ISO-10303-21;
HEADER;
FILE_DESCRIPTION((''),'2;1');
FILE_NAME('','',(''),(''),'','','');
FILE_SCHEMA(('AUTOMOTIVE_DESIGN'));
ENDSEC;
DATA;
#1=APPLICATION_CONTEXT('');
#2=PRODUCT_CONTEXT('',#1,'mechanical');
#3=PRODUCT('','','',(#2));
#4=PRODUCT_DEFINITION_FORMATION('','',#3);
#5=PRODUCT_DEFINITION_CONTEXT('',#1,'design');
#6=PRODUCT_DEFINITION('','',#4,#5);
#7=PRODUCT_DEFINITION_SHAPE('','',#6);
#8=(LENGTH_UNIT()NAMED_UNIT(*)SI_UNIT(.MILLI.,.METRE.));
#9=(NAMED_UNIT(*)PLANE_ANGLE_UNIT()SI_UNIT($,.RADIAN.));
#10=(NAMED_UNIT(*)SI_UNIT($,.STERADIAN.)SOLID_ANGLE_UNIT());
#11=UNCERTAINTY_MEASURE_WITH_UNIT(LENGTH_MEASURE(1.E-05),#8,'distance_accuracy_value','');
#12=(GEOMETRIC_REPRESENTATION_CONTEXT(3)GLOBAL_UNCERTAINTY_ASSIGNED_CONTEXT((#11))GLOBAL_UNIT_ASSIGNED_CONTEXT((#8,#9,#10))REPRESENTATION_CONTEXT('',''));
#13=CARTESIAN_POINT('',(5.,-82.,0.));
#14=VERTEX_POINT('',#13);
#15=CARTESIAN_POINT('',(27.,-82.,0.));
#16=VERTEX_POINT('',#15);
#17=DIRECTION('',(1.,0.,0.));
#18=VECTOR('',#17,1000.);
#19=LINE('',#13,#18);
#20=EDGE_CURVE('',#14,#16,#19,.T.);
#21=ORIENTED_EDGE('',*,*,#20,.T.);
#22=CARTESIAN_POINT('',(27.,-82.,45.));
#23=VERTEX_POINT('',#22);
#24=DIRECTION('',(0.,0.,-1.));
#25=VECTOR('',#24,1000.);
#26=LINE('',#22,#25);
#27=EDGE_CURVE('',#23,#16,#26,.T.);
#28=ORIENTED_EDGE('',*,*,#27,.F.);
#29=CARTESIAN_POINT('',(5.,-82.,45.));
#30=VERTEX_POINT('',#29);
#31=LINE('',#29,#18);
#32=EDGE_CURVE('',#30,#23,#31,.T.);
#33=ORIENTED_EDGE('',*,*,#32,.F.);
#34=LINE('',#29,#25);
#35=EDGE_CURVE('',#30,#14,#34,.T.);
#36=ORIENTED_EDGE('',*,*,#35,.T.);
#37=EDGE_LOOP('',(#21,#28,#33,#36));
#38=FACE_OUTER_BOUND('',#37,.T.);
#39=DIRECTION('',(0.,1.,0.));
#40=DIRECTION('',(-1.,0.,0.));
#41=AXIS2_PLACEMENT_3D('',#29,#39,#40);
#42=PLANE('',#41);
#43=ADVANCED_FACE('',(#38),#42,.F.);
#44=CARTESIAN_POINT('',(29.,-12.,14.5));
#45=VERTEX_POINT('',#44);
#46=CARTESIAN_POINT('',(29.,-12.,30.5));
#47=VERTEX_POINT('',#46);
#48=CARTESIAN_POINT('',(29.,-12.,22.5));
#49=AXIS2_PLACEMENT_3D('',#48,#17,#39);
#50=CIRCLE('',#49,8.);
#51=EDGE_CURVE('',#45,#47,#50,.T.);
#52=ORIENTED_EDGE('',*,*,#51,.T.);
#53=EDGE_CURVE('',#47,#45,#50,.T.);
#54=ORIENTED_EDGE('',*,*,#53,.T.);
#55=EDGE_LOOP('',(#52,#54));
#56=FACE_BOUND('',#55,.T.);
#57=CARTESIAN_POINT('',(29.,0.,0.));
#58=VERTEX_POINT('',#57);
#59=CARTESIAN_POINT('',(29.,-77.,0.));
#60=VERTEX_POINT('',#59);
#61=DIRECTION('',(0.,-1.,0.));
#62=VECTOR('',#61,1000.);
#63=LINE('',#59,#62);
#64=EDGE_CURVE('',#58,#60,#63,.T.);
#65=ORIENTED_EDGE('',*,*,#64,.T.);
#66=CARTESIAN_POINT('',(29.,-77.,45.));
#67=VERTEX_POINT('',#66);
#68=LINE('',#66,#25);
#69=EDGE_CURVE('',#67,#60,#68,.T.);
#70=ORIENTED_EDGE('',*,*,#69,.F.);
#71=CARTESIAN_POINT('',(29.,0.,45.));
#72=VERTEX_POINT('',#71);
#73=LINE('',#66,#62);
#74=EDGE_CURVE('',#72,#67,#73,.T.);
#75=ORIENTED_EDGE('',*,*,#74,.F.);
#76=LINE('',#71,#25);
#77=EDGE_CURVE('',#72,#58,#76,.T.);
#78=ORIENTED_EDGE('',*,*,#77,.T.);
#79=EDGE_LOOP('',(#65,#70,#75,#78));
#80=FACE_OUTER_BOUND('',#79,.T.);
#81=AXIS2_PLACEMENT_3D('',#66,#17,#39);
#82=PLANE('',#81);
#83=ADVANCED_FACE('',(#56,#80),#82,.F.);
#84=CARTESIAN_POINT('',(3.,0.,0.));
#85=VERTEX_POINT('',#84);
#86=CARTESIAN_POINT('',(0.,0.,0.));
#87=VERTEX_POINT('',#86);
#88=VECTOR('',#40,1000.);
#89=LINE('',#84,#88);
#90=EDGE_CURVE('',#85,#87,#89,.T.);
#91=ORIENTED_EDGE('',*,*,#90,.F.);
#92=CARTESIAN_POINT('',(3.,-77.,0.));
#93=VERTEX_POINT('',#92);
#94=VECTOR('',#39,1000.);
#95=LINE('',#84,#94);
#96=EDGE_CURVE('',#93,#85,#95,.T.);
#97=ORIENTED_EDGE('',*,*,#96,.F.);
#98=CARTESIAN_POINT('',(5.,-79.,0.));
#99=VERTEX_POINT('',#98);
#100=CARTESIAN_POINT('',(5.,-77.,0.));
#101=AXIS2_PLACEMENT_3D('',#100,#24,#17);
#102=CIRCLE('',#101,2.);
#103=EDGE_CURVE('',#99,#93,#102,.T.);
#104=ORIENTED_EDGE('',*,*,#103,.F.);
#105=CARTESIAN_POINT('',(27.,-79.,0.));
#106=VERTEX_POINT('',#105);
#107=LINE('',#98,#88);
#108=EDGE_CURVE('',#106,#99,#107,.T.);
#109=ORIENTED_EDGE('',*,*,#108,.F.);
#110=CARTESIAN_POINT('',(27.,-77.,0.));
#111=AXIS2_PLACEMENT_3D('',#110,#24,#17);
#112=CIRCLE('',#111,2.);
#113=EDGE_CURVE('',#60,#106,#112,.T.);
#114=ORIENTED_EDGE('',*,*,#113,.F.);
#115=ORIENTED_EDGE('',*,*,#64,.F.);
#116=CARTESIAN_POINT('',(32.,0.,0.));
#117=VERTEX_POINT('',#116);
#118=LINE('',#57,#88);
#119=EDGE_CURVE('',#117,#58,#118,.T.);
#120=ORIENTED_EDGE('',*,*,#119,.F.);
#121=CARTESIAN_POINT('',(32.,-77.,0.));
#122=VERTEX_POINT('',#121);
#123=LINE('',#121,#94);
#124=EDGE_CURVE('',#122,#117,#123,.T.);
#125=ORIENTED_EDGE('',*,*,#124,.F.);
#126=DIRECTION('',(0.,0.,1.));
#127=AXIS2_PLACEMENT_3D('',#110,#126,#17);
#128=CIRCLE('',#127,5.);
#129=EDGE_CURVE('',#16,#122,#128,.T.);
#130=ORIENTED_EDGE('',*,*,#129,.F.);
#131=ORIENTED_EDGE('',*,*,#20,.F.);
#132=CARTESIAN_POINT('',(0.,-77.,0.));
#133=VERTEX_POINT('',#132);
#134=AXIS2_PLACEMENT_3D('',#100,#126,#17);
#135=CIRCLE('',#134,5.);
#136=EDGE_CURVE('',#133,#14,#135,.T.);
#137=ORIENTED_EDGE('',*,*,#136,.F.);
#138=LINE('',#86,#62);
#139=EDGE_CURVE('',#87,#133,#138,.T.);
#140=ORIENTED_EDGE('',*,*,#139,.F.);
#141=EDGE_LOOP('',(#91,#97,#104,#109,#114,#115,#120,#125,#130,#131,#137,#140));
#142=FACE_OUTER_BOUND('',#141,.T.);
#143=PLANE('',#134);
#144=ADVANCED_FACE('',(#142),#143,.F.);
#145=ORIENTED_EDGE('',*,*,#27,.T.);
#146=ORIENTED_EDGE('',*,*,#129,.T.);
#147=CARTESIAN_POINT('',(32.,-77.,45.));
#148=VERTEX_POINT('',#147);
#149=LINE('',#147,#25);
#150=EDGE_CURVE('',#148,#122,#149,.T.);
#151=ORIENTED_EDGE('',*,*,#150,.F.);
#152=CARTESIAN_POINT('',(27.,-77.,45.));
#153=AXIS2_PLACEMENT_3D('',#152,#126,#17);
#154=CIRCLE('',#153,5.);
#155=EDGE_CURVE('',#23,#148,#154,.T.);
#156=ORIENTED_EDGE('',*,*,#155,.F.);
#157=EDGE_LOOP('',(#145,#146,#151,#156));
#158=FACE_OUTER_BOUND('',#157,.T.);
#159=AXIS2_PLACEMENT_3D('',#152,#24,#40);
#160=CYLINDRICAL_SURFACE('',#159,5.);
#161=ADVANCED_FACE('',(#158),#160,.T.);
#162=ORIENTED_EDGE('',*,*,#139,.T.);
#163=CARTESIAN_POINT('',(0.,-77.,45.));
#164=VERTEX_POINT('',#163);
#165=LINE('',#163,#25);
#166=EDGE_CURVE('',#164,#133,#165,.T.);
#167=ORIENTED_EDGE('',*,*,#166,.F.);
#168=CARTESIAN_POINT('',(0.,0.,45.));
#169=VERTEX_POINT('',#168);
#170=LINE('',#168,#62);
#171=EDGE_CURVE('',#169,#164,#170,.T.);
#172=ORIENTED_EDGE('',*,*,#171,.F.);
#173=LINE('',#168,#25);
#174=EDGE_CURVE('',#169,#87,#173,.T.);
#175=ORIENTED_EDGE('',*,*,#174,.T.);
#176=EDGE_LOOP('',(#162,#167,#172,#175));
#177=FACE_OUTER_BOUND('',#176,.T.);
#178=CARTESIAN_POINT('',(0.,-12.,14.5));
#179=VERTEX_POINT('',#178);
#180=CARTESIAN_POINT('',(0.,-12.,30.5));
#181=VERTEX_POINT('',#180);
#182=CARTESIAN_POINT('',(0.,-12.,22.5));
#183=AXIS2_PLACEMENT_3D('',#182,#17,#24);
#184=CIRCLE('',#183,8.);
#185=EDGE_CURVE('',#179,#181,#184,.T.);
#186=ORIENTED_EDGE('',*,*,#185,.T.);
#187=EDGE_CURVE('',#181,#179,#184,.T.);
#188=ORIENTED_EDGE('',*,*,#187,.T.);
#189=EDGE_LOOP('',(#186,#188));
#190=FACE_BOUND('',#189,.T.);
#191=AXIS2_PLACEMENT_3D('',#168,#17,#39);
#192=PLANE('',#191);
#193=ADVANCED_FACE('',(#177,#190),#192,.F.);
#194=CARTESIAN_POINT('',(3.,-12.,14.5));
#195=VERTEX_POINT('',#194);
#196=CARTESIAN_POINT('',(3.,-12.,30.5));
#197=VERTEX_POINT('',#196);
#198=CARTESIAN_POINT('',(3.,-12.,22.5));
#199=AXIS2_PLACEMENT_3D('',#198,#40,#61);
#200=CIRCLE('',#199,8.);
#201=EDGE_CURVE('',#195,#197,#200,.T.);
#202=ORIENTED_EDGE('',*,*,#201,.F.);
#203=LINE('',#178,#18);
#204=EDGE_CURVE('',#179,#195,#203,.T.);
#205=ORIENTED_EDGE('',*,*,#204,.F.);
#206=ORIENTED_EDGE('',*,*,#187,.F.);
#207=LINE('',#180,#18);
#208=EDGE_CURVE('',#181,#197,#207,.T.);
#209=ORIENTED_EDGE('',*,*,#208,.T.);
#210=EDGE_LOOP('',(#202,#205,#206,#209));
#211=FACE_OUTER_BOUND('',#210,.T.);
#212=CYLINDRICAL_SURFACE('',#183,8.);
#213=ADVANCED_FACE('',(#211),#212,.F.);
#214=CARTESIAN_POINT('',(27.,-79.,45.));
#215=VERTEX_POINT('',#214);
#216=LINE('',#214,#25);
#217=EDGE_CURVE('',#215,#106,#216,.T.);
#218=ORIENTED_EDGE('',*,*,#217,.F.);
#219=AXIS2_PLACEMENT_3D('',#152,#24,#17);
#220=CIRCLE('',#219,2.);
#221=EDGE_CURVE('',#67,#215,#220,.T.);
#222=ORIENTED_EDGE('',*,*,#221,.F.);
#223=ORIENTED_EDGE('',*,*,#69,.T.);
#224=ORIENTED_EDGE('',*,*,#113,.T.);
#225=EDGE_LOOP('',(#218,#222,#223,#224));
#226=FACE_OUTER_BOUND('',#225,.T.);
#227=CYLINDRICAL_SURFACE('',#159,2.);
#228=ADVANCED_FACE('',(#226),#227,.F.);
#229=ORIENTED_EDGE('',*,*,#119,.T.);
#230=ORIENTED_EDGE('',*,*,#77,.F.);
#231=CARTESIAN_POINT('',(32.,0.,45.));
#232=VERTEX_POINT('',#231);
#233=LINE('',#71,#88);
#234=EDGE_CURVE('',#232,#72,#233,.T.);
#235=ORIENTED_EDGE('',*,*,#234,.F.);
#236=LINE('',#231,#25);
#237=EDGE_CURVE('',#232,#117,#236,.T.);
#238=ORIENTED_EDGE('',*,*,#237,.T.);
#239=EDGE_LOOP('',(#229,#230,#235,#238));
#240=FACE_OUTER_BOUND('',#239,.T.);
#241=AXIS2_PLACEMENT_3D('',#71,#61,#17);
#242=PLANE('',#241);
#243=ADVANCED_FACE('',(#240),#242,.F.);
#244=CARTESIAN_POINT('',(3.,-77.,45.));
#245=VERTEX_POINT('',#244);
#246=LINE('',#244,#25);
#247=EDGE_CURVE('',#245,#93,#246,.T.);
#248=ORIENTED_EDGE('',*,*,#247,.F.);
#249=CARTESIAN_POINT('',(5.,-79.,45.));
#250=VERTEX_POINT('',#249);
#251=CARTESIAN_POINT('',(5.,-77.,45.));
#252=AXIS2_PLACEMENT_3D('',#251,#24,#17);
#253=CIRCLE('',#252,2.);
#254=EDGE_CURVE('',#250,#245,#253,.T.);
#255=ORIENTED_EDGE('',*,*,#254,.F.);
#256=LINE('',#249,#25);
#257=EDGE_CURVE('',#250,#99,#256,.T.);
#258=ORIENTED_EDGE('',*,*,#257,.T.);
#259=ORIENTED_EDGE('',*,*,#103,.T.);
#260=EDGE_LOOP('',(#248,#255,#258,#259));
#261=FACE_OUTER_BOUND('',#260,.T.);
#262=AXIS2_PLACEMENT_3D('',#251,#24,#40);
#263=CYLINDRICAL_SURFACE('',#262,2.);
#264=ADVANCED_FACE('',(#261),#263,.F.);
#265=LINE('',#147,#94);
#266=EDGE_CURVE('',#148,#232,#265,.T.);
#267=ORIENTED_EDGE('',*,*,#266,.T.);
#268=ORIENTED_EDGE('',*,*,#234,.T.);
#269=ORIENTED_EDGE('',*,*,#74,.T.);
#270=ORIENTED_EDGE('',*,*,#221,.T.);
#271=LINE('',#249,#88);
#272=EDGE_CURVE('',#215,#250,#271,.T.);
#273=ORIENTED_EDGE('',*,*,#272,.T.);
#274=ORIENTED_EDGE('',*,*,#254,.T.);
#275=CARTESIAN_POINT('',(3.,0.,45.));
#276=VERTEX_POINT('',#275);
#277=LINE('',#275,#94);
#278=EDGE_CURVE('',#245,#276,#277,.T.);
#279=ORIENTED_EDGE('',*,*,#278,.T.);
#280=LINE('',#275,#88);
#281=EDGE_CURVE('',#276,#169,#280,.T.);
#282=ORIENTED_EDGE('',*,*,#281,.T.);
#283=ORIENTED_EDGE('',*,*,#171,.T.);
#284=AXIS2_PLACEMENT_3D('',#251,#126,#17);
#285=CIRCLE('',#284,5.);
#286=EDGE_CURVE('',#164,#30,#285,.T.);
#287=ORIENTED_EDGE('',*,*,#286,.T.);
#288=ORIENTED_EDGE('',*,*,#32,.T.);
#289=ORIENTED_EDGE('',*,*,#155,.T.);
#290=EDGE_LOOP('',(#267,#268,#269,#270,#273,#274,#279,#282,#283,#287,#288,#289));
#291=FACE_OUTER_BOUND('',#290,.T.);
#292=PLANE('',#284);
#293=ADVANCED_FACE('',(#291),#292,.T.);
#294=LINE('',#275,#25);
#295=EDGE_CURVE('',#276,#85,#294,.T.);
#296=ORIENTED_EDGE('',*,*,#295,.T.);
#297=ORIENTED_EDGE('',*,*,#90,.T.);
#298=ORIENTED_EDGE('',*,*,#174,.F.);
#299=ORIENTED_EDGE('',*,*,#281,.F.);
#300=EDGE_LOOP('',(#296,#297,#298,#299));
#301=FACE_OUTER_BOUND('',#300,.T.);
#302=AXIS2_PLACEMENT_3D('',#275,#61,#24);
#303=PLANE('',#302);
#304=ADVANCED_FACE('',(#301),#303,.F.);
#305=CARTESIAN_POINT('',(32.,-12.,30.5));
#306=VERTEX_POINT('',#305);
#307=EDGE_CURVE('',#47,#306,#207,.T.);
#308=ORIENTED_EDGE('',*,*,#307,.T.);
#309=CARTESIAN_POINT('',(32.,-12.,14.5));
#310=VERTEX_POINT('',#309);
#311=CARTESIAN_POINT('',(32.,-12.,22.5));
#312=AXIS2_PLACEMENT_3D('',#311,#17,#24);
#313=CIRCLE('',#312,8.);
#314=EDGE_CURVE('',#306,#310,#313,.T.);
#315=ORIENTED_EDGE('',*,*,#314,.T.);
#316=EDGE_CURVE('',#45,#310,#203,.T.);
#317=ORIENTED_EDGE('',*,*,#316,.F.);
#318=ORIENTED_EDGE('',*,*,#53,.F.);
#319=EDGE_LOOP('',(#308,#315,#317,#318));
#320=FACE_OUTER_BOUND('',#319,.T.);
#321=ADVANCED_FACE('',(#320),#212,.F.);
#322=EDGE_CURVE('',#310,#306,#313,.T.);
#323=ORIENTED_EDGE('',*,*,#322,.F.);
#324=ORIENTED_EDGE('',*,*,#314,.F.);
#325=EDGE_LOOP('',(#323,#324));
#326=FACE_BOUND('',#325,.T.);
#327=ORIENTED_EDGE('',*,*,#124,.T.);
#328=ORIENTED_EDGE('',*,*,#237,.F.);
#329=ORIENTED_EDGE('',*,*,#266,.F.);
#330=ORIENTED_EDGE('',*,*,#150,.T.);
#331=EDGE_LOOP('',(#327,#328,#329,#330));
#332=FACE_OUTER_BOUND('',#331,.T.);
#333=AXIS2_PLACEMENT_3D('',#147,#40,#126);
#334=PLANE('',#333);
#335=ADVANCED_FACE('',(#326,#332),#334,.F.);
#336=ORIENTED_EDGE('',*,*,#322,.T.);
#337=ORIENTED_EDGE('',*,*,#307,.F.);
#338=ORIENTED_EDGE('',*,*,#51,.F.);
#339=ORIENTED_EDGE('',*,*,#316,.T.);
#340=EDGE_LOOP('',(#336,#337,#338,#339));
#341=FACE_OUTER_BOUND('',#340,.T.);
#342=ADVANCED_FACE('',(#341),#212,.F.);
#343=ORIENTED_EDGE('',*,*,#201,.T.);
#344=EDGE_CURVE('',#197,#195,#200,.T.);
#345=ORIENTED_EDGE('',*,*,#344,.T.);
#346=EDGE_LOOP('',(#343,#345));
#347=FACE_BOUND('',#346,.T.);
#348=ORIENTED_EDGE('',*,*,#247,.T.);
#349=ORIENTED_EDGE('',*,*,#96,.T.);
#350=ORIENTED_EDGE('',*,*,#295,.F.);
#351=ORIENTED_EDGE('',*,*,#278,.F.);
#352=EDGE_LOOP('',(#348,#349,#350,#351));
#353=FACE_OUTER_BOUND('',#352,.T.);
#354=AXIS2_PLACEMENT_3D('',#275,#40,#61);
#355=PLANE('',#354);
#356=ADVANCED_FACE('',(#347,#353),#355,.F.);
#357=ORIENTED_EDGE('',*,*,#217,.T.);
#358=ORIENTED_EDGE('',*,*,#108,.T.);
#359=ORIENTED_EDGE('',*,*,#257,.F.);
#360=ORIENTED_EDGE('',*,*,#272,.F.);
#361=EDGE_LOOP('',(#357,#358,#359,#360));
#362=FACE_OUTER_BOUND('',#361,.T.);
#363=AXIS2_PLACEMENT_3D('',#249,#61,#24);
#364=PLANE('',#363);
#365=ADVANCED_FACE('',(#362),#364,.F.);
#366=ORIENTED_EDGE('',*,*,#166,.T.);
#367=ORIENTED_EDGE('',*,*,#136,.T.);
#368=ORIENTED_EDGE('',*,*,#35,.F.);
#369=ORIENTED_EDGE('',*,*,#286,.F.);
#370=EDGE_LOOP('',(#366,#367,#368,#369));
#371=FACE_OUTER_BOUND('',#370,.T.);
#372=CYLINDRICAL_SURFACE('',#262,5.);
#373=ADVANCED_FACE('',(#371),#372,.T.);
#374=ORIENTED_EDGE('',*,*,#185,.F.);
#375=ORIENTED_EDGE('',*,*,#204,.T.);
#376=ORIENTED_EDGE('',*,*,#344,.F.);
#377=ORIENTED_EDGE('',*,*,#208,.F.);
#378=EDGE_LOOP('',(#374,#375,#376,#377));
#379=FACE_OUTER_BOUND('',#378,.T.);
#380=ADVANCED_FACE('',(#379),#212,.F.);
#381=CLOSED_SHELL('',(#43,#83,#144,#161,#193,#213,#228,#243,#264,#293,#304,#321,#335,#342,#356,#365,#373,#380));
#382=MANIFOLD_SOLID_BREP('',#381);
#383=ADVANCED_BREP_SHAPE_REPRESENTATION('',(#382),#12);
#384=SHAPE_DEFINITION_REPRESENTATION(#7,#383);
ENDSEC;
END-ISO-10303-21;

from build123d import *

# Parameters (mm, degrees)
BOSS_EXTRUDE1_DEPTH = 45
SKETCH2_R           = 8
CUT_EXTRUDE1_DEPTH  = 99.858484714


with BuildPart() as part:
    # Sketch1 → Boss-Extrude1 (new body)
    with BuildSketch(Plane.XY):
        with BuildLine():
            Line((0, 0), (0, -77))
            ThreePointArc((0, -77), (1.464466094, -80.535533906), (5, -82))
            Line((5, -82), (27, -82))
            ThreePointArc((27, -82), (30.535533906, -80.535533906), (32, -77))
            Line((32, -77), (32, 0))
            Line((32, 0), (29, 0))
            Line((29, 0), (29, -77))
            ThreePointArc((29, -77), (28.414213562, -78.414213562), (27, -79))
            Line((27, -79), (5, -79))
            ThreePointArc((5, -79), (3.585786438, -78.414213562), (3, -77))
            Line((3, -77), (3, 0))
            Line((3, 0), (0, 0))
        make_face()
    extrude(amount=BOSS_EXTRUDE1_DEPTH)

    # Sketch2 → Cut-Extrude1 (cut, through all)
    with BuildSketch(Plane(origin=(32, 0, 0), x_dir=(0, 0, -1), z_dir=(1, 0, 0))):
        with Locations((-22.5, -12)):
            Circle(SKETCH2_R)
    extrude(amount=-CUT_EXTRUDE1_DEPTH, mode=Mode.SUBTRACT)


solid = part.part
